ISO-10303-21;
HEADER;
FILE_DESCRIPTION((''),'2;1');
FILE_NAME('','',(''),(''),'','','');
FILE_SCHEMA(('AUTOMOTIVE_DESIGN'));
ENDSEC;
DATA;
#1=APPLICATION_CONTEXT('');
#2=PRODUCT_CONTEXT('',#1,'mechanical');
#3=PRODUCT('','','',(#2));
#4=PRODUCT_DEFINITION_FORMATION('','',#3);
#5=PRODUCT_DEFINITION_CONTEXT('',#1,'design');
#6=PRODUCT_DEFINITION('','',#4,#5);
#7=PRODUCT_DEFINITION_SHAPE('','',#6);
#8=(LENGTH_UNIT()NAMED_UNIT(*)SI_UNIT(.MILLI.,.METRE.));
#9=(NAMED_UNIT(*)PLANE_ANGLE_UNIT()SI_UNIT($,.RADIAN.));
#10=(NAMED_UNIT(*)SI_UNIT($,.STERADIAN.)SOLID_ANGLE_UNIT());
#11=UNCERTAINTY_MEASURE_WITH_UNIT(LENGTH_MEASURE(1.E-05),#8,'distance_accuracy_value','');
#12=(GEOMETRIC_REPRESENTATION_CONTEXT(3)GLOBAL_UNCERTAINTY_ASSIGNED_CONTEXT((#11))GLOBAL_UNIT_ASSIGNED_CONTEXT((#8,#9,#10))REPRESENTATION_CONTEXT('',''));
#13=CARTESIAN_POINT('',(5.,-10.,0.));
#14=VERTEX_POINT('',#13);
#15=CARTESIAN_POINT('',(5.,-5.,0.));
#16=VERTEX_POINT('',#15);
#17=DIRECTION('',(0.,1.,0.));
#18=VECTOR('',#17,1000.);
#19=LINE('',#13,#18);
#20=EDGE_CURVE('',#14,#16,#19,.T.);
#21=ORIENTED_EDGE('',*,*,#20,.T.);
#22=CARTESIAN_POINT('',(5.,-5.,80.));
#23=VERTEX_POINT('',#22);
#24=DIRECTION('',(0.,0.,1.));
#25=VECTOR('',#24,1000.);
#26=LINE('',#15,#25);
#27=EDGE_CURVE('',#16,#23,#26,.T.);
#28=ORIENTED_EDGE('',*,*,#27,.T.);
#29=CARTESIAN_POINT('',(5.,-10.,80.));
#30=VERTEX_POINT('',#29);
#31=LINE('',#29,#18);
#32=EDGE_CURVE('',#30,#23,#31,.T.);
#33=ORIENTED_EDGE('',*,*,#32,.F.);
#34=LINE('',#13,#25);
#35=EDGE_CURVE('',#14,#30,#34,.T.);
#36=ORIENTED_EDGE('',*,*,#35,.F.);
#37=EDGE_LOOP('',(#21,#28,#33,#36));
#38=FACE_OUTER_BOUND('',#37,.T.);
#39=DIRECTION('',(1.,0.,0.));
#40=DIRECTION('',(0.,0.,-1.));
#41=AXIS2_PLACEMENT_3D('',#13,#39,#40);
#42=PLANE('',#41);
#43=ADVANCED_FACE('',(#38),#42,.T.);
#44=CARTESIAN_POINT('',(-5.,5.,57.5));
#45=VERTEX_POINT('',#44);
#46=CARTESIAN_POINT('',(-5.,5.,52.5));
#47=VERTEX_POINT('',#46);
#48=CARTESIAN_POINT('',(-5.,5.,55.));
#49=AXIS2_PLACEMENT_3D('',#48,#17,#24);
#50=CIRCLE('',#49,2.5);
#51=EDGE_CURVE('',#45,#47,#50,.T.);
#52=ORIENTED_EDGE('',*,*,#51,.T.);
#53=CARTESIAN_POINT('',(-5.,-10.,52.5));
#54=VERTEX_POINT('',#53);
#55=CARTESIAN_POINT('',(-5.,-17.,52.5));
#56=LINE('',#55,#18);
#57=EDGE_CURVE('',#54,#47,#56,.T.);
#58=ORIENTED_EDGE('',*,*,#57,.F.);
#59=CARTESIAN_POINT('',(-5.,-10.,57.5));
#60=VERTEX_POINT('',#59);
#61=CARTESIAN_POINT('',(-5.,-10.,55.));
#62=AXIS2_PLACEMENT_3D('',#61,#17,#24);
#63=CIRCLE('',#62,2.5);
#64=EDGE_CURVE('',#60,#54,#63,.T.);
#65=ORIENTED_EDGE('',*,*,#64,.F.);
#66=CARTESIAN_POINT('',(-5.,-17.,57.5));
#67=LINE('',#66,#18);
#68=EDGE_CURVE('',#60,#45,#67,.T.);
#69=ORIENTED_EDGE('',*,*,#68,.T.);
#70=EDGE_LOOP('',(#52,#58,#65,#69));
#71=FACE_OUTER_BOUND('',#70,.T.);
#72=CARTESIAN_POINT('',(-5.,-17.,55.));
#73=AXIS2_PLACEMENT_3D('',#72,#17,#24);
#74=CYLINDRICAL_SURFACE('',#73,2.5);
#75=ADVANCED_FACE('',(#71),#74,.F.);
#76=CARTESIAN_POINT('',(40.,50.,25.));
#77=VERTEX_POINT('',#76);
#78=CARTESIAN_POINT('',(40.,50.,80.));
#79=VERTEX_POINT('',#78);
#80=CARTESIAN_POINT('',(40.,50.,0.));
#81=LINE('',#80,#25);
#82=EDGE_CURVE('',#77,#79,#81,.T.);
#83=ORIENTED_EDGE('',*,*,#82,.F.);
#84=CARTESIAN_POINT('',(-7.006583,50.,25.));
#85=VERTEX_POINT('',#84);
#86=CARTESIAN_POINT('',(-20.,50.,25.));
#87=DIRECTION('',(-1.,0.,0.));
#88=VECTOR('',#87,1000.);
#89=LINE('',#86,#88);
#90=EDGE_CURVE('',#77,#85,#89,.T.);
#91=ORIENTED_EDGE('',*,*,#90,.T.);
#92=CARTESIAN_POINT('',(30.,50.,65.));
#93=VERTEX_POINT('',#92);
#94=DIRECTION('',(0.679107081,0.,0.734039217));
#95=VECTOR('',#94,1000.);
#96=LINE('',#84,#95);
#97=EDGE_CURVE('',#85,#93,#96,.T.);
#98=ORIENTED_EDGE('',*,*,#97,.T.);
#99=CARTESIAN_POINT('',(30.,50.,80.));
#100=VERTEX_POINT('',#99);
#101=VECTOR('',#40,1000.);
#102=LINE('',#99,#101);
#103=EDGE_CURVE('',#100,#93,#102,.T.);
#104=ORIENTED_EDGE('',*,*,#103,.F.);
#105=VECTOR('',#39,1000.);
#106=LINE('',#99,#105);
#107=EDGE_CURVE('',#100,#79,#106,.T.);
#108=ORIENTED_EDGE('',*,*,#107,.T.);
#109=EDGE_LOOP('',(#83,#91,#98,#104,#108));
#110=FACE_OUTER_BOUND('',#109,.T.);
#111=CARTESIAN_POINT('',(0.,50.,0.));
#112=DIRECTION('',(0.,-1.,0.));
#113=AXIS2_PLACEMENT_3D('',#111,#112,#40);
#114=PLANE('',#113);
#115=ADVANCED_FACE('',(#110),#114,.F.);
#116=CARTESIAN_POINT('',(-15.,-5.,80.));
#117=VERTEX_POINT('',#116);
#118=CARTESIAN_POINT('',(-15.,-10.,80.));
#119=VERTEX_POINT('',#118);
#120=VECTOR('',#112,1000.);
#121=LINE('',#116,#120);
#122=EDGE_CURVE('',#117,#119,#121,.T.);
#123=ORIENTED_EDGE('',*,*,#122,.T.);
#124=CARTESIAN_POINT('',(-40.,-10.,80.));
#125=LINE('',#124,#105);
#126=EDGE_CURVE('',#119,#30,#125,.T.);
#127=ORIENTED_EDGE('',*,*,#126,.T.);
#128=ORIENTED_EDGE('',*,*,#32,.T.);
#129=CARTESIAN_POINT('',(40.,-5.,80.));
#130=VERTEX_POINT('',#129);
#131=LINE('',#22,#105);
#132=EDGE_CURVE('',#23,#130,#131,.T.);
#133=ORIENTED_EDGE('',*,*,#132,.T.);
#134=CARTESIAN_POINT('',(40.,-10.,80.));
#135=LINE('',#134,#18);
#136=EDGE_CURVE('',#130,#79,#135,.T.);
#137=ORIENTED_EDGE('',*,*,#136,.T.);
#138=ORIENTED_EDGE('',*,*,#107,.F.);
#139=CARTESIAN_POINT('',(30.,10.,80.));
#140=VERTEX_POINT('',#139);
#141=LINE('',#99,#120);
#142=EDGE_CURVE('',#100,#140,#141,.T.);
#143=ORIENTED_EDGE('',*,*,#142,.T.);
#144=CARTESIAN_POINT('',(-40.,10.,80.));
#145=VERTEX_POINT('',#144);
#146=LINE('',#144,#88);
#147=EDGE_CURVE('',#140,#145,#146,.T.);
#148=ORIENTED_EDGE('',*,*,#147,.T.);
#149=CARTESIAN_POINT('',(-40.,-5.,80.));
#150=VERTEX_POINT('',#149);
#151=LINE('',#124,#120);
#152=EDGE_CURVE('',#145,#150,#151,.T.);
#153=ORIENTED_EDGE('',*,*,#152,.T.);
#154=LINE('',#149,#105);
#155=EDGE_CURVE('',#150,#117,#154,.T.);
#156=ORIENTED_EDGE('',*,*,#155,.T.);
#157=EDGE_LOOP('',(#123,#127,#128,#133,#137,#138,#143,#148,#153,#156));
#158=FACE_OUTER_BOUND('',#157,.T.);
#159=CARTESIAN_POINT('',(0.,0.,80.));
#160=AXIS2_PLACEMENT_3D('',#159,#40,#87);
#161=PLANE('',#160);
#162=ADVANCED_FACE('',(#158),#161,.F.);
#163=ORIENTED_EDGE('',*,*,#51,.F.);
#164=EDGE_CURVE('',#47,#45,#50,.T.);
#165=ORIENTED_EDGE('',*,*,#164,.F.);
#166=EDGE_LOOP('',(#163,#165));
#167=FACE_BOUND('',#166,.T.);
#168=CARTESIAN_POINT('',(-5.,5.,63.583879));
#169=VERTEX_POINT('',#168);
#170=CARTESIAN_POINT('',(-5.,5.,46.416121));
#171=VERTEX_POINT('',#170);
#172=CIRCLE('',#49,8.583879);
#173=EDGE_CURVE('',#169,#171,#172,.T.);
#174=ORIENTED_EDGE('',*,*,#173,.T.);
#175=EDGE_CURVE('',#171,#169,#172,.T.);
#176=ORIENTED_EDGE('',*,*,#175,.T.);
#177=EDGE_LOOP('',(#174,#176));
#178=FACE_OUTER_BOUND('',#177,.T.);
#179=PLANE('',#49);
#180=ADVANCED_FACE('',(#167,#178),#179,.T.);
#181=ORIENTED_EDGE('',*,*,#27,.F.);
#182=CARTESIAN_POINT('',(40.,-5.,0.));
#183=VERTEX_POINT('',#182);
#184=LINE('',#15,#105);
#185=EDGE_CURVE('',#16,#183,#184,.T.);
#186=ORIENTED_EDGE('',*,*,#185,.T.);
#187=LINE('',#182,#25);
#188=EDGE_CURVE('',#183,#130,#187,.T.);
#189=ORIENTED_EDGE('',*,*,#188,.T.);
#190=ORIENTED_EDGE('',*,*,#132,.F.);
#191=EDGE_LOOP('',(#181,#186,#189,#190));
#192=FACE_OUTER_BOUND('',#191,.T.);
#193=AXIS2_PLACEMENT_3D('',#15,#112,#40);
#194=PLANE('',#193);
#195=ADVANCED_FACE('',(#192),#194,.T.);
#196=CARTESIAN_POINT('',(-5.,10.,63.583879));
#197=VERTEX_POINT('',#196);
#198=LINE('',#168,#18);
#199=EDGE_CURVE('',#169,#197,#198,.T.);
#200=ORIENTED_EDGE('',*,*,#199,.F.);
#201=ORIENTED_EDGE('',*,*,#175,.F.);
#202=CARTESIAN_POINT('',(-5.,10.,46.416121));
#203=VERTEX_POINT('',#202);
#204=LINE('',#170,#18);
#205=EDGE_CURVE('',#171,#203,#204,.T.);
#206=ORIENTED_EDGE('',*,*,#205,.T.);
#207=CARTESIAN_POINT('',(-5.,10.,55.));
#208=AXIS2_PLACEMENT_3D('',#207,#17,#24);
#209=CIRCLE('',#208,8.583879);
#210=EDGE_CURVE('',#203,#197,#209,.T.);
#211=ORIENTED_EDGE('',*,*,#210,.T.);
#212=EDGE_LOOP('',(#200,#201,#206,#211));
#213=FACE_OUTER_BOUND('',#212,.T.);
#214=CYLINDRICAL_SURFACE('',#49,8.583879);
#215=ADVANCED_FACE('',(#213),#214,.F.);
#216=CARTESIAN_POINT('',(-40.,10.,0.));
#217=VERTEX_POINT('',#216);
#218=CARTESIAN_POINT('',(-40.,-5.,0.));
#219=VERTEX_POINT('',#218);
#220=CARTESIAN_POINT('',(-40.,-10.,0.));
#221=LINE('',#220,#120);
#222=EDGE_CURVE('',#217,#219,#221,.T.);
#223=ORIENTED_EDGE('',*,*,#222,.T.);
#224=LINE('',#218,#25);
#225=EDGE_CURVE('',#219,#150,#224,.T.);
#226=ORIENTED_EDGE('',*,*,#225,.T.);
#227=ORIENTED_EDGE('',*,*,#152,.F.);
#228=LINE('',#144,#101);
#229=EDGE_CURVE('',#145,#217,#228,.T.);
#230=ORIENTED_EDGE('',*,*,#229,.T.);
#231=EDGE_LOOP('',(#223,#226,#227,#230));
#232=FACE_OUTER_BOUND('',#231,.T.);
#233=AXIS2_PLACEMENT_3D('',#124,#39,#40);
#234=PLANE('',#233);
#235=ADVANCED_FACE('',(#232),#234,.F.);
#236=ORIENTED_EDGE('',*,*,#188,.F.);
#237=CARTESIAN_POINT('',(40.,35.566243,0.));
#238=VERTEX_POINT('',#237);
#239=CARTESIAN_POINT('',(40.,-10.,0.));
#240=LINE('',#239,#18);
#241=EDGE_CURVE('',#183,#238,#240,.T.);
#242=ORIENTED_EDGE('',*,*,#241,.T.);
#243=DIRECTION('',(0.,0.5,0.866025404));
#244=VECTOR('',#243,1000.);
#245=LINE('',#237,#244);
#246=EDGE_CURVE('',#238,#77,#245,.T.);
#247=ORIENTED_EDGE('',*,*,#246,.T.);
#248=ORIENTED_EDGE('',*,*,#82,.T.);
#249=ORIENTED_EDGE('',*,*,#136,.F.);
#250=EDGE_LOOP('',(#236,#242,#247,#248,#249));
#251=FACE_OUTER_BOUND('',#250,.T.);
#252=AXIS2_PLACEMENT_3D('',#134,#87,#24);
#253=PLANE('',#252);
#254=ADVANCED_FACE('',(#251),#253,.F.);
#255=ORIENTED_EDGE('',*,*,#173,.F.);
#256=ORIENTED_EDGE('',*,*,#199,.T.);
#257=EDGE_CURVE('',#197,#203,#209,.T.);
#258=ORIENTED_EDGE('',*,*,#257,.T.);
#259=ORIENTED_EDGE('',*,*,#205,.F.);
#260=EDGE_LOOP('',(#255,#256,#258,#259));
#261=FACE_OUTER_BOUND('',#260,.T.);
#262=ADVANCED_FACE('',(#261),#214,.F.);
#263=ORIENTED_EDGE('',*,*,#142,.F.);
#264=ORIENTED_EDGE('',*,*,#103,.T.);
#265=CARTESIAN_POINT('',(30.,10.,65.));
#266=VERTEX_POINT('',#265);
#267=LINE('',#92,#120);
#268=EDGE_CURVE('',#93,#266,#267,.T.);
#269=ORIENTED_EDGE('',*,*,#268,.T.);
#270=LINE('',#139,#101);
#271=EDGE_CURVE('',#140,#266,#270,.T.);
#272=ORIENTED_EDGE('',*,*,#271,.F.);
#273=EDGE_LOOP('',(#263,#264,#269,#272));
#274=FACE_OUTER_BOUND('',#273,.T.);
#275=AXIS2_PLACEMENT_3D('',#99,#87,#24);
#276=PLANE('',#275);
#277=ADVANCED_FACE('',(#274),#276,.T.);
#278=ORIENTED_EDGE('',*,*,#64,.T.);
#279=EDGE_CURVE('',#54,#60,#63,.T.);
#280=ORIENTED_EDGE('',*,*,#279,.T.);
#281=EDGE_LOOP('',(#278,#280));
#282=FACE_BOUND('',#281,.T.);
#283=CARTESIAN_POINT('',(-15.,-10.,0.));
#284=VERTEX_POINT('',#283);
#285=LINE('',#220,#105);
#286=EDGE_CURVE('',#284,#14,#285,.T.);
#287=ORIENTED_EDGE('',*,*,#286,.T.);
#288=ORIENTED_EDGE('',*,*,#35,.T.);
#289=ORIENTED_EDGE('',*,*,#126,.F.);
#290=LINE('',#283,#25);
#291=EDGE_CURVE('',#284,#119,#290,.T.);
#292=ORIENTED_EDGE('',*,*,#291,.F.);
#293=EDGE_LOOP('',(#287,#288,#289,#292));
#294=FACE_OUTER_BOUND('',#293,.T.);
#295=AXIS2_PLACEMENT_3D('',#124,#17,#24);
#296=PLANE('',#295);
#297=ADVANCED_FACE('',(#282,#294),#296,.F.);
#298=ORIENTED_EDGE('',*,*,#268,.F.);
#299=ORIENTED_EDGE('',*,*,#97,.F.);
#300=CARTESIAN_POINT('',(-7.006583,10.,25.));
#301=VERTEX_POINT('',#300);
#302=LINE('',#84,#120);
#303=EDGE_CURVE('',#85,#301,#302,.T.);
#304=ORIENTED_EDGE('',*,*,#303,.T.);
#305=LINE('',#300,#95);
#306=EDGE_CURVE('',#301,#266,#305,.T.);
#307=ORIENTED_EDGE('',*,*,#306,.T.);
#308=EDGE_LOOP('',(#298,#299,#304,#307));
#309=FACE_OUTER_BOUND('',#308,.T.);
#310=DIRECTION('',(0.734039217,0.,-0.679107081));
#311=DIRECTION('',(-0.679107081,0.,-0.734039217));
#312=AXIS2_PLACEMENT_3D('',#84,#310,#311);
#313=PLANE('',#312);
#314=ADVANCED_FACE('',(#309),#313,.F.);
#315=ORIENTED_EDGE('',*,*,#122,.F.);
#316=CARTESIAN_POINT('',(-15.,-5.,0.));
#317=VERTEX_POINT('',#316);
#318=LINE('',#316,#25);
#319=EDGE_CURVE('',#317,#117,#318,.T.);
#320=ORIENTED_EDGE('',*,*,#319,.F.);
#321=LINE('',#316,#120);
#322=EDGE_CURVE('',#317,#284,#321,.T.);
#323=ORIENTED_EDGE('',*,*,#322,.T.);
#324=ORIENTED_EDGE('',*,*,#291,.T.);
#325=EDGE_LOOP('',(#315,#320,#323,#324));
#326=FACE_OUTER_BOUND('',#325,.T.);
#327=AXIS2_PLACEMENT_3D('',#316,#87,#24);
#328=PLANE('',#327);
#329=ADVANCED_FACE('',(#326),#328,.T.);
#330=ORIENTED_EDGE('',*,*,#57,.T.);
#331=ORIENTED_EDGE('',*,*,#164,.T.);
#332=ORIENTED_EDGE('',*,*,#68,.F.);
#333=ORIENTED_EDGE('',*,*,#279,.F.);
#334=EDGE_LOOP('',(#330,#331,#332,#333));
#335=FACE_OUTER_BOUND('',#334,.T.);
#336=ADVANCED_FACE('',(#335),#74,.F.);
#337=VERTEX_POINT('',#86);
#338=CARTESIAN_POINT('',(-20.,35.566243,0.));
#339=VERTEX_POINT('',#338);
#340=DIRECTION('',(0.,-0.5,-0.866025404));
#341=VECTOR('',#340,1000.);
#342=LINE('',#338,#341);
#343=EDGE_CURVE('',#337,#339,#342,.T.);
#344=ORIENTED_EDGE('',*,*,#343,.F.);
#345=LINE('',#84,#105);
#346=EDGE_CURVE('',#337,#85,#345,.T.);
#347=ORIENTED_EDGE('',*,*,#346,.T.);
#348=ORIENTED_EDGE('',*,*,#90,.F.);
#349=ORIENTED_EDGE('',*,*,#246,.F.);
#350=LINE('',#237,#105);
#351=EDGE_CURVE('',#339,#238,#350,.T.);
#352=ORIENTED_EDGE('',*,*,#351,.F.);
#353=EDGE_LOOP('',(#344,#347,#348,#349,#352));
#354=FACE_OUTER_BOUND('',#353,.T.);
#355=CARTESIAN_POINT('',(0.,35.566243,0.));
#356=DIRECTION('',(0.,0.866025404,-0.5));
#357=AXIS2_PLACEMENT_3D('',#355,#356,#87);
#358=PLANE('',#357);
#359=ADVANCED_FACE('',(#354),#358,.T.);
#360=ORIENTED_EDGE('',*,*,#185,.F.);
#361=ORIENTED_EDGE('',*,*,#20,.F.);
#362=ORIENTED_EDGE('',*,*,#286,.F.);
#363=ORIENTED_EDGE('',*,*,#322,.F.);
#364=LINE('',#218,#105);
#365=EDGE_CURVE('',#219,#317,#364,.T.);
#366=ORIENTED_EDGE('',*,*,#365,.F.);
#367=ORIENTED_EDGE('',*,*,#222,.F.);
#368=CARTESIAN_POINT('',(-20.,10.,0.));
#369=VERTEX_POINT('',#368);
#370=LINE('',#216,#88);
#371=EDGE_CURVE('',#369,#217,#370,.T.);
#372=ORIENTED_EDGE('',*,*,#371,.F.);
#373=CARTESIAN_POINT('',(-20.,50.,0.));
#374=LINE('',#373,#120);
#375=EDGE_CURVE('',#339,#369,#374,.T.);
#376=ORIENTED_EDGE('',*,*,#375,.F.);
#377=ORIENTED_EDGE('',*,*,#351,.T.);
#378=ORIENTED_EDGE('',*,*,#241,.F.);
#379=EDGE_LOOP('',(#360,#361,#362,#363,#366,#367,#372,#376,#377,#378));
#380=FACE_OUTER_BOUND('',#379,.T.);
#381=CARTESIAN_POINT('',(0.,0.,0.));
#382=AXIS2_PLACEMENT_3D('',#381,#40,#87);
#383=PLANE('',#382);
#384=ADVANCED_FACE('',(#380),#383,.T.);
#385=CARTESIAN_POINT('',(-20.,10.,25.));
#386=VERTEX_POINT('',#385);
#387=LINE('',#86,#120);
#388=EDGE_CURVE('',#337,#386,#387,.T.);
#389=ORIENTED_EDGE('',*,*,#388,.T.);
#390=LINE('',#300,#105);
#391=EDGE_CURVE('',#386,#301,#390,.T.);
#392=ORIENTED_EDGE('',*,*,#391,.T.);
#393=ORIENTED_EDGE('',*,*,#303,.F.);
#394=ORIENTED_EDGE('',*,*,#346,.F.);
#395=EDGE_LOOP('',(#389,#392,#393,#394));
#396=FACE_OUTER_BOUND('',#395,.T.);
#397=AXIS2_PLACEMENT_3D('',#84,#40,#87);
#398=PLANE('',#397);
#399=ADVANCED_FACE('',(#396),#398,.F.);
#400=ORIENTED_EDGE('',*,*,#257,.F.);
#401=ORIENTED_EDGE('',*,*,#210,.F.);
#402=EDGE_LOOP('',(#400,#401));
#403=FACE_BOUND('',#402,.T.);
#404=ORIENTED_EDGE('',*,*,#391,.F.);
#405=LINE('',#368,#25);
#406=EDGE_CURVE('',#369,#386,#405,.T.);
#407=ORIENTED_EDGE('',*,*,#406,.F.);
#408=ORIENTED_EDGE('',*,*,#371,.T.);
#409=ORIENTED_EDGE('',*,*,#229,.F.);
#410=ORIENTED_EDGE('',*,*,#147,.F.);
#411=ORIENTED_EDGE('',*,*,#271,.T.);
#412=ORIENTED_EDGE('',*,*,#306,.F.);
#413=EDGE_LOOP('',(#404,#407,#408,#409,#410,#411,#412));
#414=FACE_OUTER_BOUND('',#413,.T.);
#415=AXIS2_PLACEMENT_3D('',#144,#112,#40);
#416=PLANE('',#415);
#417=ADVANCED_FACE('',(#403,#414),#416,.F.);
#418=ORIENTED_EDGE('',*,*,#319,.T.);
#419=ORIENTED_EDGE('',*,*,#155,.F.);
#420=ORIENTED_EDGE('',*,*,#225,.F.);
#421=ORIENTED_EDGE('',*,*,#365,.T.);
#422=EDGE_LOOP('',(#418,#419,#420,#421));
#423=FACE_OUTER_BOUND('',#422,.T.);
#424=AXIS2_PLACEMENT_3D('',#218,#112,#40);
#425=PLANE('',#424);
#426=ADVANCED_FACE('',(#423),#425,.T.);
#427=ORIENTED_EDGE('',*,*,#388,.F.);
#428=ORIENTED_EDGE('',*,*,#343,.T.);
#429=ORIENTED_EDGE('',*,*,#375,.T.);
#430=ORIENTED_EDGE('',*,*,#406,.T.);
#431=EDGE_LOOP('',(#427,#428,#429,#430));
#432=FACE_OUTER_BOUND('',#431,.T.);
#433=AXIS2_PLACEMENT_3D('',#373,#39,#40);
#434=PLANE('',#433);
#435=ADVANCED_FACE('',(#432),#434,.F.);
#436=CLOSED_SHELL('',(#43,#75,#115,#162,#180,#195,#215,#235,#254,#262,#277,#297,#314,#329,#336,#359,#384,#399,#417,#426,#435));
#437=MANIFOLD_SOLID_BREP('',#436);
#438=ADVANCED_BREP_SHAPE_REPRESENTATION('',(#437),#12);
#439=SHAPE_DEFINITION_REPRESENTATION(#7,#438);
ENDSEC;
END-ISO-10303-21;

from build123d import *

# Parameters (mm, degrees)
BASE_PROFILE_SKETCH_W       = 80
BASE_PROFILE_SKETCH_H       = 20
BASE_BLOCK_DEPTH            = 80
UNDERSIDE_SLOT_SKETCH_W     = 25
UNDERSIDE_SLOT_SKETCH_H     = 5
UNDERSIDE_SLOT_SKETCH_W_2   = 35
UNDERSIDE_SLOT_DEPTH        = 80
UPRIGHT_WALL_SKETCH_W       = 10
UPRIGHT_WALL_SKETCH_H       = 80
UPRIGHT_WALL_DEPTH          = 40
SIDE_BLOCK_DEPTH            = 40
WALL_CHAMFER_25X30DEG_SIZE  = 25
WALL_CHAMFER_25X30DEG_SIZE2 = 14.43375673
COUNTERBORE_SKETCH_R        = 8.583879332
COUNTERBORE_RECESS_DEPTH    = 5
HOLE_SKETCH_R               = 2.5
HOLE_DIA5_DEPTH             = 22


with BuildPart() as part:
    # Base Profile Sketch → Base Block (new body)
    with BuildSketch(Plane.XY):
        Rectangle(BASE_PROFILE_SKETCH_W, BASE_PROFILE_SKETCH_H)
    extrude(amount=BASE_BLOCK_DEPTH)

    # Underside Slot Sketch → Underside Slot (cut)
    with BuildSketch(Plane.XY.offset(80)):
        with Locations((-27.5, -7.5)):
            Rectangle(UNDERSIDE_SLOT_SKETCH_W, UNDERSIDE_SLOT_SKETCH_H)
        with Locations((22.5, -7.5)):
            Rectangle(UNDERSIDE_SLOT_SKETCH_W_2, UNDERSIDE_SLOT_SKETCH_H)
    extrude(amount=-UNDERSIDE_SLOT_DEPTH, mode=Mode.SUBTRACT)

    # Upright Wall Sketch → Upright Wall (add)
    with BuildSketch(Plane(origin=(0, 10, 0), x_dir=(1, 0, 0), z_dir=(0, 1, 0))):
        with Locations((35, -40)):
            Rectangle(UPRIGHT_WALL_SKETCH_W, UPRIGHT_WALL_SKETCH_H)
    extrude(amount=UPRIGHT_WALL_DEPTH)

    # Side Block Sketch → Side Block (add)
    with BuildSketch(Plane(origin=(0, 10, 0), x_dir=(1, 0, 0), z_dir=(0, 1, 0))):
        Polygon((-20, 0), (-20, -25), (-7.006583052, -25), (30, -65), (30, 0), align=None)
    extrude(amount=SIDE_BLOCK_DEPTH)

    # Wall Chamfer 25x30deg
    wall_chamfer_25x30deg_edges = [part.edges().sort_by_distance(p)[0] for p in [
        (10, 50, 0),
    ]]
    wall_chamfer_25x30deg_side = [part.faces().sort_by_distance(p)[0] for p in [
        (16.961219392, 50, 27.237680119),
    ]]
    chamfer(wall_chamfer_25x30deg_edges, length=WALL_CHAMFER_25X30DEG_SIZE, length2=WALL_CHAMFER_25X30DEG_SIZE2, reference=wall_chamfer_25x30deg_side[0])

    # Counterbore Sketch → Counterbore Recess (cut)
    with BuildSketch(Plane(origin=(0, 10, 0), x_dir=(1, 0, 0), z_dir=(0, 1, 0))):
        with Locations(Location((-5, -55, 0), (0, 0, 270))):
            Circle(COUNTERBORE_SKETCH_R)
    extrude(amount=-COUNTERBORE_RECESS_DEPTH, mode=Mode.SUBTRACT)

    # Hole Sketch → Hole Dia5 (cut)
    with BuildSketch(Plane(origin=(0, 5, 0), x_dir=(1, 0, 0), z_dir=(0, 1, 0))):
        with Locations(Location((-5, -55, 0), (0, 0, 270))):
            Circle(HOLE_SKETCH_R)
    extrude(amount=-HOLE_DIA5_DEPTH, mode=Mode.SUBTRACT)


solid = part.part
